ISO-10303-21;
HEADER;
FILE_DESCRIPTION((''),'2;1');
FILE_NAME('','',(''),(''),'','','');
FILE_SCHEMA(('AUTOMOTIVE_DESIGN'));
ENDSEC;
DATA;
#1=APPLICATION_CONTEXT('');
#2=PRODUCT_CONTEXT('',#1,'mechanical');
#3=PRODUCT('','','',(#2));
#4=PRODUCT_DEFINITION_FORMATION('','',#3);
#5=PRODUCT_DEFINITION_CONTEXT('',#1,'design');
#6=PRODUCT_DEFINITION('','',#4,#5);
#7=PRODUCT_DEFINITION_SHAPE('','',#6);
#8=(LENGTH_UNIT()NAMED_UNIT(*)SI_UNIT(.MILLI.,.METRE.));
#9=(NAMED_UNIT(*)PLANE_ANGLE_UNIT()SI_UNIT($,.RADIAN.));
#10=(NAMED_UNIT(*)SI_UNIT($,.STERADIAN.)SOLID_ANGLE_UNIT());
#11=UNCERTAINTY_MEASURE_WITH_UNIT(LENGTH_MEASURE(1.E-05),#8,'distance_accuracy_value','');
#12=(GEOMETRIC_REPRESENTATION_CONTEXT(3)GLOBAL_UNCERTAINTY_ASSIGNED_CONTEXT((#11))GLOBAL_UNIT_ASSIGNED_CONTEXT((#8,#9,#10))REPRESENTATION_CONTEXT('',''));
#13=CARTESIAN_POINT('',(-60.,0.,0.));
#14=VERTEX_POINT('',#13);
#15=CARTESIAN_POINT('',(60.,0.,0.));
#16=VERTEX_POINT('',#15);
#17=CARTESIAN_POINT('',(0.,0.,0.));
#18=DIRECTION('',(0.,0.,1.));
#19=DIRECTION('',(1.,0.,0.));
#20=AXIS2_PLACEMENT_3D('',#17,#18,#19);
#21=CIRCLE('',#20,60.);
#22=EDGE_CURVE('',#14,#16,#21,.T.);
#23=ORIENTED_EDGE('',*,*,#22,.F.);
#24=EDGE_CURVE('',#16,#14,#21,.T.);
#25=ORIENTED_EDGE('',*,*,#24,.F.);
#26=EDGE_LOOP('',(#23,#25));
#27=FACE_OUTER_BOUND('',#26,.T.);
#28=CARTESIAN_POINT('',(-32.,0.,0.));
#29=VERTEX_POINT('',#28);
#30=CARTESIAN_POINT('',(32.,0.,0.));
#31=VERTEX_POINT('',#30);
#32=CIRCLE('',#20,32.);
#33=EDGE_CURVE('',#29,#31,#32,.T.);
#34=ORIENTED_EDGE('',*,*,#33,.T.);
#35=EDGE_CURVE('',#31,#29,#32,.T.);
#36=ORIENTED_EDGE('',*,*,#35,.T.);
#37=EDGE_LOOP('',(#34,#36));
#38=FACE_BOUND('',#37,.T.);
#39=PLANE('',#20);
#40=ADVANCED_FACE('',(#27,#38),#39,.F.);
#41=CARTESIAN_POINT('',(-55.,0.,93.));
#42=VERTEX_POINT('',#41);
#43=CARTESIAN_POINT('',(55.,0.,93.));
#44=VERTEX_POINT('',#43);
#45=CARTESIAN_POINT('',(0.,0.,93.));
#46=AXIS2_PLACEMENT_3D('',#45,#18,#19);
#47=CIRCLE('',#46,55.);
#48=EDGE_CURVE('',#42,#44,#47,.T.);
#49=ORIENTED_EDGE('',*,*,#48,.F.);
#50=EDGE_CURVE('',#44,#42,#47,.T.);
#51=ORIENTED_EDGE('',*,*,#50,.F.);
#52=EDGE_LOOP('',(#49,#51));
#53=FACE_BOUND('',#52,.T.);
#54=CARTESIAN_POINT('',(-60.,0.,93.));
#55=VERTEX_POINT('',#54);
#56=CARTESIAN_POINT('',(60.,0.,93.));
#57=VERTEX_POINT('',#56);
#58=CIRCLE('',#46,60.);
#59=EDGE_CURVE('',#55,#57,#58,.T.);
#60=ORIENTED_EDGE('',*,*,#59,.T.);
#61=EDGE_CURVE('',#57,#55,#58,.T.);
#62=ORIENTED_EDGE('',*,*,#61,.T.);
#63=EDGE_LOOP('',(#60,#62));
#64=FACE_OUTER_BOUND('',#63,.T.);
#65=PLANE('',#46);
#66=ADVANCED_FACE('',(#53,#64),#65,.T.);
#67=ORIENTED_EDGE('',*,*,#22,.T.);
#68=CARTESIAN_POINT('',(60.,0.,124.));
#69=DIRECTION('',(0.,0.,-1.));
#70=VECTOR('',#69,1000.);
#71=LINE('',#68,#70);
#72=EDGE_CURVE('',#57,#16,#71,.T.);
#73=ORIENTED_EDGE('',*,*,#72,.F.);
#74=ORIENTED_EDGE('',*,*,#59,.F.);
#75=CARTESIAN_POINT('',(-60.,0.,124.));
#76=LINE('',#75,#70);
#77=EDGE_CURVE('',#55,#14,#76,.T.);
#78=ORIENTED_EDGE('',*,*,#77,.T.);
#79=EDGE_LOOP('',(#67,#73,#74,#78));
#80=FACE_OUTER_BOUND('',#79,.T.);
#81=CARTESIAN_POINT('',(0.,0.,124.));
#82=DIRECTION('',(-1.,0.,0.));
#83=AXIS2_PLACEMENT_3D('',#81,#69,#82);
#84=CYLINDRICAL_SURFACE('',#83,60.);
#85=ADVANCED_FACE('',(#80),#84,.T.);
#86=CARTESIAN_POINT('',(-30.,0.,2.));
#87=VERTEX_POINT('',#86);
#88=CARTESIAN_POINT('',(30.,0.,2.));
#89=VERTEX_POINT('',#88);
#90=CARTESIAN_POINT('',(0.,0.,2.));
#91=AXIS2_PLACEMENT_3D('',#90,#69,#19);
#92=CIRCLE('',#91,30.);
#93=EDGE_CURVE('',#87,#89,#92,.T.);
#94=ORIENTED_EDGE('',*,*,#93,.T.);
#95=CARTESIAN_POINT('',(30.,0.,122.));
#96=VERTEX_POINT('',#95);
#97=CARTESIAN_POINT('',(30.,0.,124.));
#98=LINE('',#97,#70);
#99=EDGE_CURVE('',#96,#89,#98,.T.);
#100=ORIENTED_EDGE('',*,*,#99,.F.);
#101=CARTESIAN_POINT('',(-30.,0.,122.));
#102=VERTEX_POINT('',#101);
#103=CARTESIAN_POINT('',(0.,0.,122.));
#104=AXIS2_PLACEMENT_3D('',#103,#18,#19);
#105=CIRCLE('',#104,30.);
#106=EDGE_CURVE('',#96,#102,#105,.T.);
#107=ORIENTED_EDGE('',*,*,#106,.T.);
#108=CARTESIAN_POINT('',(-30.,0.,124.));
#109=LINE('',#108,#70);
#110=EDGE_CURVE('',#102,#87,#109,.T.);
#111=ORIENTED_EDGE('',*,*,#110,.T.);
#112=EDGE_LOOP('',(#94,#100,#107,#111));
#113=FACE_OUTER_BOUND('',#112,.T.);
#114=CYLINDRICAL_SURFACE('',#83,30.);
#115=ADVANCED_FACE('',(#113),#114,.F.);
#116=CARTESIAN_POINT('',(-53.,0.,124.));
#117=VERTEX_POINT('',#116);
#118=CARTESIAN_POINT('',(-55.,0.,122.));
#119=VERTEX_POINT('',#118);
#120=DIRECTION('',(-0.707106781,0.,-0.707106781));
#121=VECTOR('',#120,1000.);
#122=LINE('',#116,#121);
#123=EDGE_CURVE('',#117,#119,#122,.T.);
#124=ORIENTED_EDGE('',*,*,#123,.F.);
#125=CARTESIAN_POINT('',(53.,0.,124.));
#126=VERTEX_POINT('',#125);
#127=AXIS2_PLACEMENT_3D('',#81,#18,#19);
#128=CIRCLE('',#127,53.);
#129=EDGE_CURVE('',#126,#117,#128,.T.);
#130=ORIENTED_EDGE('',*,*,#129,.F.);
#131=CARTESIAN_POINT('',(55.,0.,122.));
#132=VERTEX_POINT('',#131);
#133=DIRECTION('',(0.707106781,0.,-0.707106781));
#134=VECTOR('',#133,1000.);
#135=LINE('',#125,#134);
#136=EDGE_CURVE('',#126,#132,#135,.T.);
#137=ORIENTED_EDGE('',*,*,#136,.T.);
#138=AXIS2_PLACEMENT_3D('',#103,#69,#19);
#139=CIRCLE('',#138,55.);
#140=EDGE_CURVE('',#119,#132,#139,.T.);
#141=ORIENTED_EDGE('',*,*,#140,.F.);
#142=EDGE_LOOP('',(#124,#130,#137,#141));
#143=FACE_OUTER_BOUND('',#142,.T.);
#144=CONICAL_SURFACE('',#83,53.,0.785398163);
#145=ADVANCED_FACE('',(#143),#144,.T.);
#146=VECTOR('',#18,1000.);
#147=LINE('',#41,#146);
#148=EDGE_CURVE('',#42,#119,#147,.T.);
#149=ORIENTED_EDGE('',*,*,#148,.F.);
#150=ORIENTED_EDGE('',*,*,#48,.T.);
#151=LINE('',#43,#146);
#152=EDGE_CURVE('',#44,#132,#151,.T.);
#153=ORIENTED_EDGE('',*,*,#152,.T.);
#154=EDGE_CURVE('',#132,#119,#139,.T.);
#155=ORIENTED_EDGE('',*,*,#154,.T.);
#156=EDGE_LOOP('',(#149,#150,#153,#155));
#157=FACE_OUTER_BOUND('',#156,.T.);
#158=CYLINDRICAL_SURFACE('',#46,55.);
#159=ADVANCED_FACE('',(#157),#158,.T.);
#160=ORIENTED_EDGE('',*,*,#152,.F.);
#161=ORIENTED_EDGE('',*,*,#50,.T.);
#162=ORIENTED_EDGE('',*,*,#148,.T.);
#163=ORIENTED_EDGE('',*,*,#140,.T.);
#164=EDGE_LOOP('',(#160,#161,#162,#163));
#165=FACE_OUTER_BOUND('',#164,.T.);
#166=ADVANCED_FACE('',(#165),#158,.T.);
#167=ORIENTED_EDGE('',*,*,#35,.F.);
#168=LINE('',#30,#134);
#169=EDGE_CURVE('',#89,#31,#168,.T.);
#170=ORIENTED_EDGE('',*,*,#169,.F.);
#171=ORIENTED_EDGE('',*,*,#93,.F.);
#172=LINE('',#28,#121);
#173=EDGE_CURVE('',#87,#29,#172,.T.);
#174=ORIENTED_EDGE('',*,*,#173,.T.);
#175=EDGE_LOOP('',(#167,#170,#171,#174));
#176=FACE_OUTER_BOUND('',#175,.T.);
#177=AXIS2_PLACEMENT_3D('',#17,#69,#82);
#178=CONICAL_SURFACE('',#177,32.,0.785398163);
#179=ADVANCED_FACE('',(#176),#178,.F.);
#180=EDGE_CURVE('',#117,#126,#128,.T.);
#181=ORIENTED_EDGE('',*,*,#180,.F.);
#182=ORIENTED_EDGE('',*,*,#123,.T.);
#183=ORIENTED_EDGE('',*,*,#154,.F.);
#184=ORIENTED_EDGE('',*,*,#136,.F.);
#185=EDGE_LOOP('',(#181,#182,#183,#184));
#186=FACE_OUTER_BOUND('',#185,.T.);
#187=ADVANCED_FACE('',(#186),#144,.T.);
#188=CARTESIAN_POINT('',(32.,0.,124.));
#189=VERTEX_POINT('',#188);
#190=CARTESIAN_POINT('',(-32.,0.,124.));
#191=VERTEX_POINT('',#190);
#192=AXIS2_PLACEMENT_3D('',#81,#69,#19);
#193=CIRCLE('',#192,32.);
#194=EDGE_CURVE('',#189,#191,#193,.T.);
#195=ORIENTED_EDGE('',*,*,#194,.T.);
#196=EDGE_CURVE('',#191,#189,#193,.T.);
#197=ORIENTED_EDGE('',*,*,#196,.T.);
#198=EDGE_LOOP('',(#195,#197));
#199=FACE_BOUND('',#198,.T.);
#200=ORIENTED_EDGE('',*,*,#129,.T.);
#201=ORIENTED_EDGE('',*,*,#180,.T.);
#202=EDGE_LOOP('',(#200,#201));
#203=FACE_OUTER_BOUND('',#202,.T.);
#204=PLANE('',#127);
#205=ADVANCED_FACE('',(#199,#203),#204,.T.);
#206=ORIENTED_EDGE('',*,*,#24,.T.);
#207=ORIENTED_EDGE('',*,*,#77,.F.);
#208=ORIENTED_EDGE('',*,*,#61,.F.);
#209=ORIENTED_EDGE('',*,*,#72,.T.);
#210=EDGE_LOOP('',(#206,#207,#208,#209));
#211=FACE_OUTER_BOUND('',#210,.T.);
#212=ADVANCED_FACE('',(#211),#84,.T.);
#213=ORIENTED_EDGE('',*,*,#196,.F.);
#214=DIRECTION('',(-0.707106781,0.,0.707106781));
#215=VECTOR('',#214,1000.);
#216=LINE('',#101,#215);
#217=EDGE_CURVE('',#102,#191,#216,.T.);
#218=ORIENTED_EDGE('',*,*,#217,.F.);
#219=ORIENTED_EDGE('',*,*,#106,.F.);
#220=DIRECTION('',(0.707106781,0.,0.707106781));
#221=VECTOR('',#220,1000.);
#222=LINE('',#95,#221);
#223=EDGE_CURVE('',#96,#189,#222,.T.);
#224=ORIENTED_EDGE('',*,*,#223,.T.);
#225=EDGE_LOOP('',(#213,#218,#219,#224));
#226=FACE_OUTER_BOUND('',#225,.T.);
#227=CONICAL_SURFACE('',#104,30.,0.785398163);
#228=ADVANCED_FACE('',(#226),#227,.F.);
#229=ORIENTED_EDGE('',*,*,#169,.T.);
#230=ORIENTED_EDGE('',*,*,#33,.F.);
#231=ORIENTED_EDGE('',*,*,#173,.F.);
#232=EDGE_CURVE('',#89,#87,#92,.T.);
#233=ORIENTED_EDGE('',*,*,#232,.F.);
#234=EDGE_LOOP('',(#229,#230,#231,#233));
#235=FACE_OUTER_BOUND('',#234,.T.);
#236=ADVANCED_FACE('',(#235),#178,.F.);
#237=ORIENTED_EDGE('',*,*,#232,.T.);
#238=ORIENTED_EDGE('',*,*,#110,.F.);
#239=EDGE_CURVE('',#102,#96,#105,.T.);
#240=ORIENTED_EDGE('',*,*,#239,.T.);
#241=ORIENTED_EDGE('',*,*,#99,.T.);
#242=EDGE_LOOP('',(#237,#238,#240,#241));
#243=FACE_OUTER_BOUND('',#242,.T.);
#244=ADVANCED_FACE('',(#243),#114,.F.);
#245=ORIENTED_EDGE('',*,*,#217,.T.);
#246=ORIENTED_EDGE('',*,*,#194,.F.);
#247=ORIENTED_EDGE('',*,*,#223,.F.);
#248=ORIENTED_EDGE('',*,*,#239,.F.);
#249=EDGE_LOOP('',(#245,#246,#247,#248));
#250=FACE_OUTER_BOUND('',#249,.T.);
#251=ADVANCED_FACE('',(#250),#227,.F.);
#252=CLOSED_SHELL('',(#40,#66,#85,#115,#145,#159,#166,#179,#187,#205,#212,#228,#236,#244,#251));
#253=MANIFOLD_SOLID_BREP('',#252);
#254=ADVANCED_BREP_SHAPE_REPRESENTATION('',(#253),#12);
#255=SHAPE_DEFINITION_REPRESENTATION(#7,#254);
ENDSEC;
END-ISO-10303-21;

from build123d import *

# Parameters (mm, degrees)
SKETCH1_R           = 60
SKETCH1_R_2         = 30
BOSS_EXTRUDE1_DEPTH = 124
CUT_EXTRUDE1_START  = -31
SKETCH2_R           = 60
SKETCH2_R_2         = 55
CUT_EXTRUDE1_DEPTH  = 31
CHAMFER1_SIZE       = 2


with BuildPart() as part:
    # Sketch1 → Boss-Extrude1 (new body)
    with BuildSketch(Plane.XY):
        Circle(SKETCH1_R)
        Circle(SKETCH1_R_2, mode=Mode.SUBTRACT)
    extrude(amount=BOSS_EXTRUDE1_DEPTH)

    # Sketch2 → Cut-Extrude1 (cut)
    with BuildSketch(Plane.XY.offset(124).offset(CUT_EXTRUDE1_START)):
        Circle(SKETCH2_R)
        Circle(SKETCH2_R_2, mode=Mode.SUBTRACT)
    extrude(amount=CUT_EXTRUDE1_DEPTH, mode=Mode.SUBTRACT)

    # Chamfer1
    chamfer1_edges = [part.edges().sort_by_distance(p)[0] for p in [
        (-55, 0, 124),
        (-30, 0, 0),
        (-30, 0, 124),
    ]]
    chamfer(chamfer1_edges, length=CHAMFER1_SIZE)


solid = part.part
